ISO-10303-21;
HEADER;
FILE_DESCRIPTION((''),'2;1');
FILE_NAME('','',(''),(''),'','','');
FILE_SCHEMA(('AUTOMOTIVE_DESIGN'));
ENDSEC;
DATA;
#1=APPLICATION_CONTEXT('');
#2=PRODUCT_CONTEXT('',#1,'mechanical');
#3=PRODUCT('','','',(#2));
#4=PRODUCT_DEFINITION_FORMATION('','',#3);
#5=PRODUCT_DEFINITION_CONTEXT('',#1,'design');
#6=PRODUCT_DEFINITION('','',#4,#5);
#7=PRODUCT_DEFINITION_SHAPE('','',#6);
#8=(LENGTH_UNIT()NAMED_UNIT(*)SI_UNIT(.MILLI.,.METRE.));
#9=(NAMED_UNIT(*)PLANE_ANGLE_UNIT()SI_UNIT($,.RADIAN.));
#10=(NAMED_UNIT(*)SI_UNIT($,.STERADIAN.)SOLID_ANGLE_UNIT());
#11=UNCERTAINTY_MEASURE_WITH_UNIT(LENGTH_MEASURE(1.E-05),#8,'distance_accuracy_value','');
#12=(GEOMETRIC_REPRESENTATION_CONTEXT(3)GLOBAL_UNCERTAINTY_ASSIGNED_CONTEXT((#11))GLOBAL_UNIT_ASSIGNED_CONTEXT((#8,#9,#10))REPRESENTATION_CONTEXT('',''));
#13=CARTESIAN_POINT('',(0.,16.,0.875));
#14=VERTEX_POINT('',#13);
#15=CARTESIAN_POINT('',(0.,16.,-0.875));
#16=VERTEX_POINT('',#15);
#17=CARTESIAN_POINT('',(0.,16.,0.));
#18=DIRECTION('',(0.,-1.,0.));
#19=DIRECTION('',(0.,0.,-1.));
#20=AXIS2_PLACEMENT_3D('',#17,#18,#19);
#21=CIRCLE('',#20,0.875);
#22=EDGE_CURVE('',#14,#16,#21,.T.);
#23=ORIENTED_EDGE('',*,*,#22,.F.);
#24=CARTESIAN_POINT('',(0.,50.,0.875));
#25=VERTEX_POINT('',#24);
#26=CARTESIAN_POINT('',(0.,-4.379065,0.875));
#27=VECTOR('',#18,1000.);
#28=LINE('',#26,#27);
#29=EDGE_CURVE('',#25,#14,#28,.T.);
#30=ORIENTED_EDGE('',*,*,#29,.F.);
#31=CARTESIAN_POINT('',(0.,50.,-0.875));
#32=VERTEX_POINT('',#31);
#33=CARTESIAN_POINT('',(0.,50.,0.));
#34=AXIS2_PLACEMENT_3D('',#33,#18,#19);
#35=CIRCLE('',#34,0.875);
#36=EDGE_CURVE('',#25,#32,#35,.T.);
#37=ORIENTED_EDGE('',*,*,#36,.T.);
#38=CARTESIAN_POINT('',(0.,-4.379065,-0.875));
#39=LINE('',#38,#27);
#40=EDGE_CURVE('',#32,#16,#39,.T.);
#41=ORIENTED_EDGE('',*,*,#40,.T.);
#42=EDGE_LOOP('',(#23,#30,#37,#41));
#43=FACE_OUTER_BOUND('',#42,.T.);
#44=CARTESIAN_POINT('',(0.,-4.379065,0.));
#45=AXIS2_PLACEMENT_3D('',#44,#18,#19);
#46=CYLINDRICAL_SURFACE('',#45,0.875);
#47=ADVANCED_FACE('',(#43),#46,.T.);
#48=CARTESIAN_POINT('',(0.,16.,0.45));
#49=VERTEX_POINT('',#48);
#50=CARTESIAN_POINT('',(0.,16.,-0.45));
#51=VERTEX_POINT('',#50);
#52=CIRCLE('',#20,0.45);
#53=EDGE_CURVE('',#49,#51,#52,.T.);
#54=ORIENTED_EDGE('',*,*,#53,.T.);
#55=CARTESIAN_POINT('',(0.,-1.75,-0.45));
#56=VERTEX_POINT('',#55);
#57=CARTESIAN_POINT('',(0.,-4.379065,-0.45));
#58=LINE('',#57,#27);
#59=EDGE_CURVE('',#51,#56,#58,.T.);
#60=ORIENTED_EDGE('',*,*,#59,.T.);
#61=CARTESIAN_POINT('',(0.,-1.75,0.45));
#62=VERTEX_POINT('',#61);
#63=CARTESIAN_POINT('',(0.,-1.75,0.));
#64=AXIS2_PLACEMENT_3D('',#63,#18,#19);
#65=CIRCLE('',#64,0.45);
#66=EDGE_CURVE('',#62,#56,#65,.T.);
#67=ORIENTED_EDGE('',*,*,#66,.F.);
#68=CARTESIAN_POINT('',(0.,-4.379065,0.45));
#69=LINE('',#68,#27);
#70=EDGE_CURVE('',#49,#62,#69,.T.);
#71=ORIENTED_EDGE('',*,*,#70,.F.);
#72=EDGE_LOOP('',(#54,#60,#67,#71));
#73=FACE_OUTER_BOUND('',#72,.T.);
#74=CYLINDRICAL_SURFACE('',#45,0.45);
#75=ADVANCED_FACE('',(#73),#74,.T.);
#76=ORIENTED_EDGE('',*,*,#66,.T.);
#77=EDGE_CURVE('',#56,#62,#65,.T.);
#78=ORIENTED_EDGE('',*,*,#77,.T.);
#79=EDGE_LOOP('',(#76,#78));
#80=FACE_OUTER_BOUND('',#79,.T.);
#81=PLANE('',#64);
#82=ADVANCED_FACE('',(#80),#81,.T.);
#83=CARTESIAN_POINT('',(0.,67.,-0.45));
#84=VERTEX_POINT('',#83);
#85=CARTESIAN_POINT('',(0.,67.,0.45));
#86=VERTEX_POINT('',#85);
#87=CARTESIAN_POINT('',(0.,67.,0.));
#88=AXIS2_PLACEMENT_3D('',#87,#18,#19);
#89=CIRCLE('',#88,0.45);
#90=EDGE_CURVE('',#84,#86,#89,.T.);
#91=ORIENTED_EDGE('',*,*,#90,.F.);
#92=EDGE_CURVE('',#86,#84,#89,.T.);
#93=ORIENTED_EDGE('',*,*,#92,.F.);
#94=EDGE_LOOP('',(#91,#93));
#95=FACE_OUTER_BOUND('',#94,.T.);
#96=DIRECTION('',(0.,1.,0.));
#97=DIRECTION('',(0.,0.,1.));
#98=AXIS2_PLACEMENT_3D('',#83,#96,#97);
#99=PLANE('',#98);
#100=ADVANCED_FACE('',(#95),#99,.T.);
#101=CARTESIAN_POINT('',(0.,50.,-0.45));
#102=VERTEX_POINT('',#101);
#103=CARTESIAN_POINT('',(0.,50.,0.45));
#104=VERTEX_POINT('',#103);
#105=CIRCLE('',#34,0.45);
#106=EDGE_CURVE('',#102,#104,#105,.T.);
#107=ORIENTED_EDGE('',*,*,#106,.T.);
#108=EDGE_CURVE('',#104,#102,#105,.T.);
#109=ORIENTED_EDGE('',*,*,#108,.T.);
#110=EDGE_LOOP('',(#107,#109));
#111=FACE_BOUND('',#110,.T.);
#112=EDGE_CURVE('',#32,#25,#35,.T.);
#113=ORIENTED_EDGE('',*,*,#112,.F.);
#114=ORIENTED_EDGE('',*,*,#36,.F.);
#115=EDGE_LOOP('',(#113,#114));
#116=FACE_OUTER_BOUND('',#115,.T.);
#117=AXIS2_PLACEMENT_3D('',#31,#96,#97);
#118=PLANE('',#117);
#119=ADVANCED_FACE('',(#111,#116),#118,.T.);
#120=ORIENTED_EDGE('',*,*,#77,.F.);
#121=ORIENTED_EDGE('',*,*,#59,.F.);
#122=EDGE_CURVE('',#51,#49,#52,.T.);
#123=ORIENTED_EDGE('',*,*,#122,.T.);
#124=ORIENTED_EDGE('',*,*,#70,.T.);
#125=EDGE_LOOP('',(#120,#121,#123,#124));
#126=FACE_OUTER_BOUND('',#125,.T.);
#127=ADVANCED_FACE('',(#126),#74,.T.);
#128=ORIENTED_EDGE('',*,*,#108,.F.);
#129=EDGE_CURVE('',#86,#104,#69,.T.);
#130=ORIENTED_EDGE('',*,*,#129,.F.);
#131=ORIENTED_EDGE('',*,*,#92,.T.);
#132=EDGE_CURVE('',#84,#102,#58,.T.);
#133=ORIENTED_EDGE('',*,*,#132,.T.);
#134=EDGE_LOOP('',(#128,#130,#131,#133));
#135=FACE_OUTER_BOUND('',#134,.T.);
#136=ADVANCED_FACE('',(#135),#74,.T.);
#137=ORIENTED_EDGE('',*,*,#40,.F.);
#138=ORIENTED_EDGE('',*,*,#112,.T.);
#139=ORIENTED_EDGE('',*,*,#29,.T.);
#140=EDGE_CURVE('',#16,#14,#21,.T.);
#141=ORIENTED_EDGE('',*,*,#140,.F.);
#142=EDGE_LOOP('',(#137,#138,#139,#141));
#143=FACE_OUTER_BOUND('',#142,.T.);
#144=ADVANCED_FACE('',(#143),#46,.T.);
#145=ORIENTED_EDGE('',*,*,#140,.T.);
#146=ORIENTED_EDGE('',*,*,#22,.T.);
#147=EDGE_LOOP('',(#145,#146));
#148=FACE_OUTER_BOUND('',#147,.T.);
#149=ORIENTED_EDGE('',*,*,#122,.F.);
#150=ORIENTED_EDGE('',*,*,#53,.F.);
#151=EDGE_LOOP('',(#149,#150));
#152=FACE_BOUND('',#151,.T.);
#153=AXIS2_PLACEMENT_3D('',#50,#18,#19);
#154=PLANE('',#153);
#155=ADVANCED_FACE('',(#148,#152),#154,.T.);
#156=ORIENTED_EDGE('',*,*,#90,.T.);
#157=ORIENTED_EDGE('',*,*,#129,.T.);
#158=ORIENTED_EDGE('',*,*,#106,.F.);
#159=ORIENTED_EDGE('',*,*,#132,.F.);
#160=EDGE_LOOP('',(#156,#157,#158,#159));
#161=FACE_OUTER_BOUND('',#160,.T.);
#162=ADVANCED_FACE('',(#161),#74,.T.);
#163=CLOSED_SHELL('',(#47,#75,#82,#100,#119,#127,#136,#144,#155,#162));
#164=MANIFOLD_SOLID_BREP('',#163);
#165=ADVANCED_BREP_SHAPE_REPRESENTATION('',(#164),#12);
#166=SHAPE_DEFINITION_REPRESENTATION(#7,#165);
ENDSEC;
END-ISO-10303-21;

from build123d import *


with BuildPart() as part:
    # Sketch1 → Revolve1 (revolve)
    with BuildSketch(Plane(origin=(0, 0, 0), x_dir=(0, 0, -1), z_dir=(1, 0, 0))):
        Polygon((0.45, 16), (0.875, 16), (0.875, 50), (0.45, 50), (0.45, 67), (0, 67), (0, -1.75), (0.45, -1.75), align=None)
    revolve(axis=Axis((0, -4.379065135, 0), (0, 1, 0)))


solid = part.part
